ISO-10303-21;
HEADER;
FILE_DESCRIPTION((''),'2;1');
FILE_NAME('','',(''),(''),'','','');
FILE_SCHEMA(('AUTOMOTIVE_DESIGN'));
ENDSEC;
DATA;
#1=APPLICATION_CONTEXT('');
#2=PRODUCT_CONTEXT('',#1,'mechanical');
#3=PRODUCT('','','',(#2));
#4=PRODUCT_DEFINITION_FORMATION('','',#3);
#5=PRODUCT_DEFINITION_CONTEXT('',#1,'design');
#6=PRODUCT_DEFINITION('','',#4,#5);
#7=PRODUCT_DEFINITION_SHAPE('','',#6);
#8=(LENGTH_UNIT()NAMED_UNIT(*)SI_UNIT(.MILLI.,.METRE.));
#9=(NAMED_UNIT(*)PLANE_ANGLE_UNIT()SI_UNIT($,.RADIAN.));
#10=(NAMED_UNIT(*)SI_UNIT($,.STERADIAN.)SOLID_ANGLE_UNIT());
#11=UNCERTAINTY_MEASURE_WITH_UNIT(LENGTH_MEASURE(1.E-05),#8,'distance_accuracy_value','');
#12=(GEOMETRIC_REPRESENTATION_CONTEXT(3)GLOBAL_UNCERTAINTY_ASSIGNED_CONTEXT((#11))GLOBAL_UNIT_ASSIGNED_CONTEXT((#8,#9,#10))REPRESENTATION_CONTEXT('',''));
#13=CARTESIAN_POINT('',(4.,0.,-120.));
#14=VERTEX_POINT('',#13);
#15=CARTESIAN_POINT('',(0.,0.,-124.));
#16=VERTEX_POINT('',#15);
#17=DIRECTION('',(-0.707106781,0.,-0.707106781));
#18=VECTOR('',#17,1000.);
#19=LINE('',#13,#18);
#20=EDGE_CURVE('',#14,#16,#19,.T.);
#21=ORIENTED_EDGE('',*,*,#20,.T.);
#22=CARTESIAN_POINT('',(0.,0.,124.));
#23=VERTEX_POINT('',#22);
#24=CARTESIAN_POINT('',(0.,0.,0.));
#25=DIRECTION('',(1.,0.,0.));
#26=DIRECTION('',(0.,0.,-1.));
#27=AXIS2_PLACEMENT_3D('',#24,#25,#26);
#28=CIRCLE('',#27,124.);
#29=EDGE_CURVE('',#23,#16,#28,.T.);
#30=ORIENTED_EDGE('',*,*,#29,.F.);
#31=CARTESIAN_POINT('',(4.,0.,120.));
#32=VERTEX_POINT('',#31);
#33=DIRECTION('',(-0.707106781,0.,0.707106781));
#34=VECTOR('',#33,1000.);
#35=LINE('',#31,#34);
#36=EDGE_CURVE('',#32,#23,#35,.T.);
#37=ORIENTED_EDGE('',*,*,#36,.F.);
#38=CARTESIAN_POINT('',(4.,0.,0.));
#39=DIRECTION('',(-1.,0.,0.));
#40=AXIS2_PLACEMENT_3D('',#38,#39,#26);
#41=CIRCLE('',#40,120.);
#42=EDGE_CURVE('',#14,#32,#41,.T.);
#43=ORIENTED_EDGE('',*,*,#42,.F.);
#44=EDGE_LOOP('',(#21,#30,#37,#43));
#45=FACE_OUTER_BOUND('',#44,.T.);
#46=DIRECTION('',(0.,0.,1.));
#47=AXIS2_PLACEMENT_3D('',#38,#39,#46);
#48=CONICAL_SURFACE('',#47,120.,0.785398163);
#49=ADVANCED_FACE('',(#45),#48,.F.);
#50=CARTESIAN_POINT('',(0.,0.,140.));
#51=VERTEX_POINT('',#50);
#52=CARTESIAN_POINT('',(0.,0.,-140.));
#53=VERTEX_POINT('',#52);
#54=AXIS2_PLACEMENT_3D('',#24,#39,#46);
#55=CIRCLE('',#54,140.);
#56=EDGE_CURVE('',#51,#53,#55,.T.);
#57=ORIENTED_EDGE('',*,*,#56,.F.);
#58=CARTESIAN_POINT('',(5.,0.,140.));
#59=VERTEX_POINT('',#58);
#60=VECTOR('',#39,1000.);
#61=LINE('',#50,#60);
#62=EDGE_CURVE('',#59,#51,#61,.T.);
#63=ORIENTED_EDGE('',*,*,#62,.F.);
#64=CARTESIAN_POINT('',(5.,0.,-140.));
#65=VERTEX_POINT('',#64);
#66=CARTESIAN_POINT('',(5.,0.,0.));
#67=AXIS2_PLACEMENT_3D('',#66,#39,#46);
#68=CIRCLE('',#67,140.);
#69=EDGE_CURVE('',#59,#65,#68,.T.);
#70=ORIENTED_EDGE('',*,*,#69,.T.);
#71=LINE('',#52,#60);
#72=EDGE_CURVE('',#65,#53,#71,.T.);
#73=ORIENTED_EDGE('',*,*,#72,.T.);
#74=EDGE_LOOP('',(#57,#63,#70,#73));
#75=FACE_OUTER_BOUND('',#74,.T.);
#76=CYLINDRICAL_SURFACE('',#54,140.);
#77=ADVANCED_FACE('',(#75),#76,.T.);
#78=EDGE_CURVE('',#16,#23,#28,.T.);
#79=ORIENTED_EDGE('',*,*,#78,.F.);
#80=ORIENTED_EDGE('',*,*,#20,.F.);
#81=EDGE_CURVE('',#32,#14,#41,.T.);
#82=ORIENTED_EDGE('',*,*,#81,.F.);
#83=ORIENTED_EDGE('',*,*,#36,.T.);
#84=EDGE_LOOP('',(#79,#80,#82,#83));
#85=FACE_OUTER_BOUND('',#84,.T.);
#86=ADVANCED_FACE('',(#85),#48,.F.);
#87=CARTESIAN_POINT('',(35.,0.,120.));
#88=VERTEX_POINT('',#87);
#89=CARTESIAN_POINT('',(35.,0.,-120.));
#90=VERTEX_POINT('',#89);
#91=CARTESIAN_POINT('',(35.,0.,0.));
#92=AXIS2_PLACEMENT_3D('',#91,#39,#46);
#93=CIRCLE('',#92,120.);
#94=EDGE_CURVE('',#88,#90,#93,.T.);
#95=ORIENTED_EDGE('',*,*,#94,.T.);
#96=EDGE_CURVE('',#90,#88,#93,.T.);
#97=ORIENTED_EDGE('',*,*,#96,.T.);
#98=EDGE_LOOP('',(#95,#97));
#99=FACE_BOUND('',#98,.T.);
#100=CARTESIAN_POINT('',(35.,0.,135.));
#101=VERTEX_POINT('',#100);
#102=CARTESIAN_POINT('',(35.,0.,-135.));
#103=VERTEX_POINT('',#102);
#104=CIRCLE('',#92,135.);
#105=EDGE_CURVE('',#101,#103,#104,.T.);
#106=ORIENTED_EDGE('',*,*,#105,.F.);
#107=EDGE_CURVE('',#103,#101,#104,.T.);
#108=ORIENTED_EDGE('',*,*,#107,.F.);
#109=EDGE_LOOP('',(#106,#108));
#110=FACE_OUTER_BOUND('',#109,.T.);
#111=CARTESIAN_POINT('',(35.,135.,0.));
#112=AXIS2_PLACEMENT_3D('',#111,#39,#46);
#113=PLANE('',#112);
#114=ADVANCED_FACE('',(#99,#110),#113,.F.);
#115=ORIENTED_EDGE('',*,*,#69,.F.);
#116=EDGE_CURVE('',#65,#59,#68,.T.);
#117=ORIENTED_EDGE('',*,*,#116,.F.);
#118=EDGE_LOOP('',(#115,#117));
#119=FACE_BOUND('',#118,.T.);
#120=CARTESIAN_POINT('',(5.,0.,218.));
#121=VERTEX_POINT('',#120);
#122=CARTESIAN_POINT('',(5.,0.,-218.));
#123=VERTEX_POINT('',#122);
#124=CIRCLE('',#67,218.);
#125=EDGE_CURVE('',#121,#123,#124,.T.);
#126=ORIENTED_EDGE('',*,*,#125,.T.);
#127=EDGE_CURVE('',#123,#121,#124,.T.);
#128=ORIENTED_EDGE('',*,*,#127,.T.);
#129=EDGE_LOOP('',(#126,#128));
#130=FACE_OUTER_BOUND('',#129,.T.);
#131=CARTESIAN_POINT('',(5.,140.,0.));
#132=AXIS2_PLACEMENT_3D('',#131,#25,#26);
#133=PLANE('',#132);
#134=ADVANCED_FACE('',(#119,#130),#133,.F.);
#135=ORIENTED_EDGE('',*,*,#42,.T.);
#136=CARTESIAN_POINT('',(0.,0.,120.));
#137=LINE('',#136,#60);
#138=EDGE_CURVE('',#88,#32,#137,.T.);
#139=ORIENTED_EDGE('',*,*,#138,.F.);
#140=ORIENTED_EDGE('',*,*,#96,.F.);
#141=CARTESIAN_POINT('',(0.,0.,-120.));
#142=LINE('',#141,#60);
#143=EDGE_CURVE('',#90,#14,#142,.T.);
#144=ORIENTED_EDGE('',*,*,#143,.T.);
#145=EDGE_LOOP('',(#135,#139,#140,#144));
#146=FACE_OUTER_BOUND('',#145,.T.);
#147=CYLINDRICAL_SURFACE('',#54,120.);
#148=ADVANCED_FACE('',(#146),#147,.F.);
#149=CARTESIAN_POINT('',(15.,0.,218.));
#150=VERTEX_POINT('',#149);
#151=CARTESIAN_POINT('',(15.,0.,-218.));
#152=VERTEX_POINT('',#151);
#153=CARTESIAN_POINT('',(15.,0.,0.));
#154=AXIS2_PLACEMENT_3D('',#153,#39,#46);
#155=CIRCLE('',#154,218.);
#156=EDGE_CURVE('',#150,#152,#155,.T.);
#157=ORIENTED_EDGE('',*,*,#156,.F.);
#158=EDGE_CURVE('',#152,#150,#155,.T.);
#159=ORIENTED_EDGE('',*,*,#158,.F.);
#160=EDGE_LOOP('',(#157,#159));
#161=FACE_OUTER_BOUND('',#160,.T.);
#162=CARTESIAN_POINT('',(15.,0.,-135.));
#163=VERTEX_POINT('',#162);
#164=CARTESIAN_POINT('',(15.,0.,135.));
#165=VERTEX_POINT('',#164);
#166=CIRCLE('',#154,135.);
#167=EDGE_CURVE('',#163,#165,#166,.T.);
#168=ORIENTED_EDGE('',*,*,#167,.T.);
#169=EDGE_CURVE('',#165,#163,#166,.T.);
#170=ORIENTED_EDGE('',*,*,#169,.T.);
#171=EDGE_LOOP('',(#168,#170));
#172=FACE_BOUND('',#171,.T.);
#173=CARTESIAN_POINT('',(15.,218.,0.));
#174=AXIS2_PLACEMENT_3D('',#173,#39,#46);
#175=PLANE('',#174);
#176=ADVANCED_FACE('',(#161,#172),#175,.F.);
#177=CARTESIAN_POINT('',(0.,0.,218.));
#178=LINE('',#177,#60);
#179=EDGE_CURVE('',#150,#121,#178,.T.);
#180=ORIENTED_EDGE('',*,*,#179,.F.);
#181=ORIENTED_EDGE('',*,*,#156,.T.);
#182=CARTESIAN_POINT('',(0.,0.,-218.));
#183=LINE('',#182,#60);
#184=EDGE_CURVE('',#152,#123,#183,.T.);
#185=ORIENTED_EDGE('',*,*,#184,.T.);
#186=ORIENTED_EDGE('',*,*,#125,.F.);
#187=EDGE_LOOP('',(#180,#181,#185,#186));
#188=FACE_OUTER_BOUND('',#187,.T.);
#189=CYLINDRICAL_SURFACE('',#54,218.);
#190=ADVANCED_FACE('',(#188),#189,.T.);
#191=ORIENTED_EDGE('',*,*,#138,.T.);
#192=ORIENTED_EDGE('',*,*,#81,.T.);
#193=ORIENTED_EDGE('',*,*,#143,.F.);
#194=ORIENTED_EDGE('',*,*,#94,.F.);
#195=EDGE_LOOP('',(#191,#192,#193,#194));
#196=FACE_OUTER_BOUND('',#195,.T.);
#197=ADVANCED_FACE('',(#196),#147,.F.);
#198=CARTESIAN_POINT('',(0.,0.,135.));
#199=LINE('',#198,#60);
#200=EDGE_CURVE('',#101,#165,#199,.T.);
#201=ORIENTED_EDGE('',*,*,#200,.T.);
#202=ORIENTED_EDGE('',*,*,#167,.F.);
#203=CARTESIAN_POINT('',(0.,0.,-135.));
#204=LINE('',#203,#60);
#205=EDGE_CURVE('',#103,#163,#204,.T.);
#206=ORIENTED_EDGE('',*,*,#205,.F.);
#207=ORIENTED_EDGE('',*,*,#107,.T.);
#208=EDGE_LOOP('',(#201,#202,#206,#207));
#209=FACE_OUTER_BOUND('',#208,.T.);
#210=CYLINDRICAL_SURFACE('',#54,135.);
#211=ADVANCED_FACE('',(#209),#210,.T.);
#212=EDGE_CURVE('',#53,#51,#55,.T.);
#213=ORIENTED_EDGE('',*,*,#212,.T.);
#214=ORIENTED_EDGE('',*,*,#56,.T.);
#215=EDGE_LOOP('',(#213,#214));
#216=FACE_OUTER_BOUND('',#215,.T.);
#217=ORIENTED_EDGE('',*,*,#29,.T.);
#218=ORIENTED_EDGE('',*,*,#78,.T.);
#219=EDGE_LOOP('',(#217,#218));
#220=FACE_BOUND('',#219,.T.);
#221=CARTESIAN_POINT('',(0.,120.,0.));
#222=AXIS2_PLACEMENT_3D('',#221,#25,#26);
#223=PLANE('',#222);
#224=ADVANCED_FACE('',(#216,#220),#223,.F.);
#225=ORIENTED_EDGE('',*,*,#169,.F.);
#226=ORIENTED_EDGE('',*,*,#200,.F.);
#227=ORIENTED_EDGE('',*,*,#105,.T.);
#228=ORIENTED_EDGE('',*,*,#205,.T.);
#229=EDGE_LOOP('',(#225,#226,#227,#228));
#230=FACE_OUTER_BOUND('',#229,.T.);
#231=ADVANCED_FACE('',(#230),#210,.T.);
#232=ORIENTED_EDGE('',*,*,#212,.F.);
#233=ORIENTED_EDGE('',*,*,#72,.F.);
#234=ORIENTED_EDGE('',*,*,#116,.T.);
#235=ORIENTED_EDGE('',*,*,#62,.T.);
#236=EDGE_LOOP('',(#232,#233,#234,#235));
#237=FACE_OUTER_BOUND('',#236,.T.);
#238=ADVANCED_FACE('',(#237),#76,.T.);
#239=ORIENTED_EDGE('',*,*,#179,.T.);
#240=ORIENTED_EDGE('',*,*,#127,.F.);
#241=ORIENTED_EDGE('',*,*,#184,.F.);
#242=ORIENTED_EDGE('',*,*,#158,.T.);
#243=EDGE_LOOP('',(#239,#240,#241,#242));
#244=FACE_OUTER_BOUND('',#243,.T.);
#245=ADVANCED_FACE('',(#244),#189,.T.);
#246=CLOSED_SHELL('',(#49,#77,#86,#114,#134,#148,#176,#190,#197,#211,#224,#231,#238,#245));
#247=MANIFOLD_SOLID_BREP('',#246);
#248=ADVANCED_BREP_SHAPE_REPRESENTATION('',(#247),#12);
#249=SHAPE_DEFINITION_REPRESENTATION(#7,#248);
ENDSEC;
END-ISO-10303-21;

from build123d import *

# Parameters (mm, degrees)
CHAMFER1_SIZE = 4


with BuildPart() as part:
    # Sketch1 → Revolve1 (revolve)
    with BuildSketch(Plane.XY, mode=Mode.PRIVATE) as revolve1_sk:
        Polygon((0, 140), (5, 140), (5, 218), (15, 218), (15, 135), (35, 135), (35, 120), (0, 120), align=None)
    revolve(revolve1_sk.sketch.rotate(Axis((0, 0, 0), (1, 0, 0)), 90), axis=Axis((0, 0, 0), (1, 0, 0)))

    # Chamfer1
    chamfer1_edges = [part.edges().sort_by_distance(p)[0] for p in [
        (0, 0, -120),
    ]]
    chamfer(chamfer1_edges, length=CHAMFER1_SIZE)


solid = part.part
